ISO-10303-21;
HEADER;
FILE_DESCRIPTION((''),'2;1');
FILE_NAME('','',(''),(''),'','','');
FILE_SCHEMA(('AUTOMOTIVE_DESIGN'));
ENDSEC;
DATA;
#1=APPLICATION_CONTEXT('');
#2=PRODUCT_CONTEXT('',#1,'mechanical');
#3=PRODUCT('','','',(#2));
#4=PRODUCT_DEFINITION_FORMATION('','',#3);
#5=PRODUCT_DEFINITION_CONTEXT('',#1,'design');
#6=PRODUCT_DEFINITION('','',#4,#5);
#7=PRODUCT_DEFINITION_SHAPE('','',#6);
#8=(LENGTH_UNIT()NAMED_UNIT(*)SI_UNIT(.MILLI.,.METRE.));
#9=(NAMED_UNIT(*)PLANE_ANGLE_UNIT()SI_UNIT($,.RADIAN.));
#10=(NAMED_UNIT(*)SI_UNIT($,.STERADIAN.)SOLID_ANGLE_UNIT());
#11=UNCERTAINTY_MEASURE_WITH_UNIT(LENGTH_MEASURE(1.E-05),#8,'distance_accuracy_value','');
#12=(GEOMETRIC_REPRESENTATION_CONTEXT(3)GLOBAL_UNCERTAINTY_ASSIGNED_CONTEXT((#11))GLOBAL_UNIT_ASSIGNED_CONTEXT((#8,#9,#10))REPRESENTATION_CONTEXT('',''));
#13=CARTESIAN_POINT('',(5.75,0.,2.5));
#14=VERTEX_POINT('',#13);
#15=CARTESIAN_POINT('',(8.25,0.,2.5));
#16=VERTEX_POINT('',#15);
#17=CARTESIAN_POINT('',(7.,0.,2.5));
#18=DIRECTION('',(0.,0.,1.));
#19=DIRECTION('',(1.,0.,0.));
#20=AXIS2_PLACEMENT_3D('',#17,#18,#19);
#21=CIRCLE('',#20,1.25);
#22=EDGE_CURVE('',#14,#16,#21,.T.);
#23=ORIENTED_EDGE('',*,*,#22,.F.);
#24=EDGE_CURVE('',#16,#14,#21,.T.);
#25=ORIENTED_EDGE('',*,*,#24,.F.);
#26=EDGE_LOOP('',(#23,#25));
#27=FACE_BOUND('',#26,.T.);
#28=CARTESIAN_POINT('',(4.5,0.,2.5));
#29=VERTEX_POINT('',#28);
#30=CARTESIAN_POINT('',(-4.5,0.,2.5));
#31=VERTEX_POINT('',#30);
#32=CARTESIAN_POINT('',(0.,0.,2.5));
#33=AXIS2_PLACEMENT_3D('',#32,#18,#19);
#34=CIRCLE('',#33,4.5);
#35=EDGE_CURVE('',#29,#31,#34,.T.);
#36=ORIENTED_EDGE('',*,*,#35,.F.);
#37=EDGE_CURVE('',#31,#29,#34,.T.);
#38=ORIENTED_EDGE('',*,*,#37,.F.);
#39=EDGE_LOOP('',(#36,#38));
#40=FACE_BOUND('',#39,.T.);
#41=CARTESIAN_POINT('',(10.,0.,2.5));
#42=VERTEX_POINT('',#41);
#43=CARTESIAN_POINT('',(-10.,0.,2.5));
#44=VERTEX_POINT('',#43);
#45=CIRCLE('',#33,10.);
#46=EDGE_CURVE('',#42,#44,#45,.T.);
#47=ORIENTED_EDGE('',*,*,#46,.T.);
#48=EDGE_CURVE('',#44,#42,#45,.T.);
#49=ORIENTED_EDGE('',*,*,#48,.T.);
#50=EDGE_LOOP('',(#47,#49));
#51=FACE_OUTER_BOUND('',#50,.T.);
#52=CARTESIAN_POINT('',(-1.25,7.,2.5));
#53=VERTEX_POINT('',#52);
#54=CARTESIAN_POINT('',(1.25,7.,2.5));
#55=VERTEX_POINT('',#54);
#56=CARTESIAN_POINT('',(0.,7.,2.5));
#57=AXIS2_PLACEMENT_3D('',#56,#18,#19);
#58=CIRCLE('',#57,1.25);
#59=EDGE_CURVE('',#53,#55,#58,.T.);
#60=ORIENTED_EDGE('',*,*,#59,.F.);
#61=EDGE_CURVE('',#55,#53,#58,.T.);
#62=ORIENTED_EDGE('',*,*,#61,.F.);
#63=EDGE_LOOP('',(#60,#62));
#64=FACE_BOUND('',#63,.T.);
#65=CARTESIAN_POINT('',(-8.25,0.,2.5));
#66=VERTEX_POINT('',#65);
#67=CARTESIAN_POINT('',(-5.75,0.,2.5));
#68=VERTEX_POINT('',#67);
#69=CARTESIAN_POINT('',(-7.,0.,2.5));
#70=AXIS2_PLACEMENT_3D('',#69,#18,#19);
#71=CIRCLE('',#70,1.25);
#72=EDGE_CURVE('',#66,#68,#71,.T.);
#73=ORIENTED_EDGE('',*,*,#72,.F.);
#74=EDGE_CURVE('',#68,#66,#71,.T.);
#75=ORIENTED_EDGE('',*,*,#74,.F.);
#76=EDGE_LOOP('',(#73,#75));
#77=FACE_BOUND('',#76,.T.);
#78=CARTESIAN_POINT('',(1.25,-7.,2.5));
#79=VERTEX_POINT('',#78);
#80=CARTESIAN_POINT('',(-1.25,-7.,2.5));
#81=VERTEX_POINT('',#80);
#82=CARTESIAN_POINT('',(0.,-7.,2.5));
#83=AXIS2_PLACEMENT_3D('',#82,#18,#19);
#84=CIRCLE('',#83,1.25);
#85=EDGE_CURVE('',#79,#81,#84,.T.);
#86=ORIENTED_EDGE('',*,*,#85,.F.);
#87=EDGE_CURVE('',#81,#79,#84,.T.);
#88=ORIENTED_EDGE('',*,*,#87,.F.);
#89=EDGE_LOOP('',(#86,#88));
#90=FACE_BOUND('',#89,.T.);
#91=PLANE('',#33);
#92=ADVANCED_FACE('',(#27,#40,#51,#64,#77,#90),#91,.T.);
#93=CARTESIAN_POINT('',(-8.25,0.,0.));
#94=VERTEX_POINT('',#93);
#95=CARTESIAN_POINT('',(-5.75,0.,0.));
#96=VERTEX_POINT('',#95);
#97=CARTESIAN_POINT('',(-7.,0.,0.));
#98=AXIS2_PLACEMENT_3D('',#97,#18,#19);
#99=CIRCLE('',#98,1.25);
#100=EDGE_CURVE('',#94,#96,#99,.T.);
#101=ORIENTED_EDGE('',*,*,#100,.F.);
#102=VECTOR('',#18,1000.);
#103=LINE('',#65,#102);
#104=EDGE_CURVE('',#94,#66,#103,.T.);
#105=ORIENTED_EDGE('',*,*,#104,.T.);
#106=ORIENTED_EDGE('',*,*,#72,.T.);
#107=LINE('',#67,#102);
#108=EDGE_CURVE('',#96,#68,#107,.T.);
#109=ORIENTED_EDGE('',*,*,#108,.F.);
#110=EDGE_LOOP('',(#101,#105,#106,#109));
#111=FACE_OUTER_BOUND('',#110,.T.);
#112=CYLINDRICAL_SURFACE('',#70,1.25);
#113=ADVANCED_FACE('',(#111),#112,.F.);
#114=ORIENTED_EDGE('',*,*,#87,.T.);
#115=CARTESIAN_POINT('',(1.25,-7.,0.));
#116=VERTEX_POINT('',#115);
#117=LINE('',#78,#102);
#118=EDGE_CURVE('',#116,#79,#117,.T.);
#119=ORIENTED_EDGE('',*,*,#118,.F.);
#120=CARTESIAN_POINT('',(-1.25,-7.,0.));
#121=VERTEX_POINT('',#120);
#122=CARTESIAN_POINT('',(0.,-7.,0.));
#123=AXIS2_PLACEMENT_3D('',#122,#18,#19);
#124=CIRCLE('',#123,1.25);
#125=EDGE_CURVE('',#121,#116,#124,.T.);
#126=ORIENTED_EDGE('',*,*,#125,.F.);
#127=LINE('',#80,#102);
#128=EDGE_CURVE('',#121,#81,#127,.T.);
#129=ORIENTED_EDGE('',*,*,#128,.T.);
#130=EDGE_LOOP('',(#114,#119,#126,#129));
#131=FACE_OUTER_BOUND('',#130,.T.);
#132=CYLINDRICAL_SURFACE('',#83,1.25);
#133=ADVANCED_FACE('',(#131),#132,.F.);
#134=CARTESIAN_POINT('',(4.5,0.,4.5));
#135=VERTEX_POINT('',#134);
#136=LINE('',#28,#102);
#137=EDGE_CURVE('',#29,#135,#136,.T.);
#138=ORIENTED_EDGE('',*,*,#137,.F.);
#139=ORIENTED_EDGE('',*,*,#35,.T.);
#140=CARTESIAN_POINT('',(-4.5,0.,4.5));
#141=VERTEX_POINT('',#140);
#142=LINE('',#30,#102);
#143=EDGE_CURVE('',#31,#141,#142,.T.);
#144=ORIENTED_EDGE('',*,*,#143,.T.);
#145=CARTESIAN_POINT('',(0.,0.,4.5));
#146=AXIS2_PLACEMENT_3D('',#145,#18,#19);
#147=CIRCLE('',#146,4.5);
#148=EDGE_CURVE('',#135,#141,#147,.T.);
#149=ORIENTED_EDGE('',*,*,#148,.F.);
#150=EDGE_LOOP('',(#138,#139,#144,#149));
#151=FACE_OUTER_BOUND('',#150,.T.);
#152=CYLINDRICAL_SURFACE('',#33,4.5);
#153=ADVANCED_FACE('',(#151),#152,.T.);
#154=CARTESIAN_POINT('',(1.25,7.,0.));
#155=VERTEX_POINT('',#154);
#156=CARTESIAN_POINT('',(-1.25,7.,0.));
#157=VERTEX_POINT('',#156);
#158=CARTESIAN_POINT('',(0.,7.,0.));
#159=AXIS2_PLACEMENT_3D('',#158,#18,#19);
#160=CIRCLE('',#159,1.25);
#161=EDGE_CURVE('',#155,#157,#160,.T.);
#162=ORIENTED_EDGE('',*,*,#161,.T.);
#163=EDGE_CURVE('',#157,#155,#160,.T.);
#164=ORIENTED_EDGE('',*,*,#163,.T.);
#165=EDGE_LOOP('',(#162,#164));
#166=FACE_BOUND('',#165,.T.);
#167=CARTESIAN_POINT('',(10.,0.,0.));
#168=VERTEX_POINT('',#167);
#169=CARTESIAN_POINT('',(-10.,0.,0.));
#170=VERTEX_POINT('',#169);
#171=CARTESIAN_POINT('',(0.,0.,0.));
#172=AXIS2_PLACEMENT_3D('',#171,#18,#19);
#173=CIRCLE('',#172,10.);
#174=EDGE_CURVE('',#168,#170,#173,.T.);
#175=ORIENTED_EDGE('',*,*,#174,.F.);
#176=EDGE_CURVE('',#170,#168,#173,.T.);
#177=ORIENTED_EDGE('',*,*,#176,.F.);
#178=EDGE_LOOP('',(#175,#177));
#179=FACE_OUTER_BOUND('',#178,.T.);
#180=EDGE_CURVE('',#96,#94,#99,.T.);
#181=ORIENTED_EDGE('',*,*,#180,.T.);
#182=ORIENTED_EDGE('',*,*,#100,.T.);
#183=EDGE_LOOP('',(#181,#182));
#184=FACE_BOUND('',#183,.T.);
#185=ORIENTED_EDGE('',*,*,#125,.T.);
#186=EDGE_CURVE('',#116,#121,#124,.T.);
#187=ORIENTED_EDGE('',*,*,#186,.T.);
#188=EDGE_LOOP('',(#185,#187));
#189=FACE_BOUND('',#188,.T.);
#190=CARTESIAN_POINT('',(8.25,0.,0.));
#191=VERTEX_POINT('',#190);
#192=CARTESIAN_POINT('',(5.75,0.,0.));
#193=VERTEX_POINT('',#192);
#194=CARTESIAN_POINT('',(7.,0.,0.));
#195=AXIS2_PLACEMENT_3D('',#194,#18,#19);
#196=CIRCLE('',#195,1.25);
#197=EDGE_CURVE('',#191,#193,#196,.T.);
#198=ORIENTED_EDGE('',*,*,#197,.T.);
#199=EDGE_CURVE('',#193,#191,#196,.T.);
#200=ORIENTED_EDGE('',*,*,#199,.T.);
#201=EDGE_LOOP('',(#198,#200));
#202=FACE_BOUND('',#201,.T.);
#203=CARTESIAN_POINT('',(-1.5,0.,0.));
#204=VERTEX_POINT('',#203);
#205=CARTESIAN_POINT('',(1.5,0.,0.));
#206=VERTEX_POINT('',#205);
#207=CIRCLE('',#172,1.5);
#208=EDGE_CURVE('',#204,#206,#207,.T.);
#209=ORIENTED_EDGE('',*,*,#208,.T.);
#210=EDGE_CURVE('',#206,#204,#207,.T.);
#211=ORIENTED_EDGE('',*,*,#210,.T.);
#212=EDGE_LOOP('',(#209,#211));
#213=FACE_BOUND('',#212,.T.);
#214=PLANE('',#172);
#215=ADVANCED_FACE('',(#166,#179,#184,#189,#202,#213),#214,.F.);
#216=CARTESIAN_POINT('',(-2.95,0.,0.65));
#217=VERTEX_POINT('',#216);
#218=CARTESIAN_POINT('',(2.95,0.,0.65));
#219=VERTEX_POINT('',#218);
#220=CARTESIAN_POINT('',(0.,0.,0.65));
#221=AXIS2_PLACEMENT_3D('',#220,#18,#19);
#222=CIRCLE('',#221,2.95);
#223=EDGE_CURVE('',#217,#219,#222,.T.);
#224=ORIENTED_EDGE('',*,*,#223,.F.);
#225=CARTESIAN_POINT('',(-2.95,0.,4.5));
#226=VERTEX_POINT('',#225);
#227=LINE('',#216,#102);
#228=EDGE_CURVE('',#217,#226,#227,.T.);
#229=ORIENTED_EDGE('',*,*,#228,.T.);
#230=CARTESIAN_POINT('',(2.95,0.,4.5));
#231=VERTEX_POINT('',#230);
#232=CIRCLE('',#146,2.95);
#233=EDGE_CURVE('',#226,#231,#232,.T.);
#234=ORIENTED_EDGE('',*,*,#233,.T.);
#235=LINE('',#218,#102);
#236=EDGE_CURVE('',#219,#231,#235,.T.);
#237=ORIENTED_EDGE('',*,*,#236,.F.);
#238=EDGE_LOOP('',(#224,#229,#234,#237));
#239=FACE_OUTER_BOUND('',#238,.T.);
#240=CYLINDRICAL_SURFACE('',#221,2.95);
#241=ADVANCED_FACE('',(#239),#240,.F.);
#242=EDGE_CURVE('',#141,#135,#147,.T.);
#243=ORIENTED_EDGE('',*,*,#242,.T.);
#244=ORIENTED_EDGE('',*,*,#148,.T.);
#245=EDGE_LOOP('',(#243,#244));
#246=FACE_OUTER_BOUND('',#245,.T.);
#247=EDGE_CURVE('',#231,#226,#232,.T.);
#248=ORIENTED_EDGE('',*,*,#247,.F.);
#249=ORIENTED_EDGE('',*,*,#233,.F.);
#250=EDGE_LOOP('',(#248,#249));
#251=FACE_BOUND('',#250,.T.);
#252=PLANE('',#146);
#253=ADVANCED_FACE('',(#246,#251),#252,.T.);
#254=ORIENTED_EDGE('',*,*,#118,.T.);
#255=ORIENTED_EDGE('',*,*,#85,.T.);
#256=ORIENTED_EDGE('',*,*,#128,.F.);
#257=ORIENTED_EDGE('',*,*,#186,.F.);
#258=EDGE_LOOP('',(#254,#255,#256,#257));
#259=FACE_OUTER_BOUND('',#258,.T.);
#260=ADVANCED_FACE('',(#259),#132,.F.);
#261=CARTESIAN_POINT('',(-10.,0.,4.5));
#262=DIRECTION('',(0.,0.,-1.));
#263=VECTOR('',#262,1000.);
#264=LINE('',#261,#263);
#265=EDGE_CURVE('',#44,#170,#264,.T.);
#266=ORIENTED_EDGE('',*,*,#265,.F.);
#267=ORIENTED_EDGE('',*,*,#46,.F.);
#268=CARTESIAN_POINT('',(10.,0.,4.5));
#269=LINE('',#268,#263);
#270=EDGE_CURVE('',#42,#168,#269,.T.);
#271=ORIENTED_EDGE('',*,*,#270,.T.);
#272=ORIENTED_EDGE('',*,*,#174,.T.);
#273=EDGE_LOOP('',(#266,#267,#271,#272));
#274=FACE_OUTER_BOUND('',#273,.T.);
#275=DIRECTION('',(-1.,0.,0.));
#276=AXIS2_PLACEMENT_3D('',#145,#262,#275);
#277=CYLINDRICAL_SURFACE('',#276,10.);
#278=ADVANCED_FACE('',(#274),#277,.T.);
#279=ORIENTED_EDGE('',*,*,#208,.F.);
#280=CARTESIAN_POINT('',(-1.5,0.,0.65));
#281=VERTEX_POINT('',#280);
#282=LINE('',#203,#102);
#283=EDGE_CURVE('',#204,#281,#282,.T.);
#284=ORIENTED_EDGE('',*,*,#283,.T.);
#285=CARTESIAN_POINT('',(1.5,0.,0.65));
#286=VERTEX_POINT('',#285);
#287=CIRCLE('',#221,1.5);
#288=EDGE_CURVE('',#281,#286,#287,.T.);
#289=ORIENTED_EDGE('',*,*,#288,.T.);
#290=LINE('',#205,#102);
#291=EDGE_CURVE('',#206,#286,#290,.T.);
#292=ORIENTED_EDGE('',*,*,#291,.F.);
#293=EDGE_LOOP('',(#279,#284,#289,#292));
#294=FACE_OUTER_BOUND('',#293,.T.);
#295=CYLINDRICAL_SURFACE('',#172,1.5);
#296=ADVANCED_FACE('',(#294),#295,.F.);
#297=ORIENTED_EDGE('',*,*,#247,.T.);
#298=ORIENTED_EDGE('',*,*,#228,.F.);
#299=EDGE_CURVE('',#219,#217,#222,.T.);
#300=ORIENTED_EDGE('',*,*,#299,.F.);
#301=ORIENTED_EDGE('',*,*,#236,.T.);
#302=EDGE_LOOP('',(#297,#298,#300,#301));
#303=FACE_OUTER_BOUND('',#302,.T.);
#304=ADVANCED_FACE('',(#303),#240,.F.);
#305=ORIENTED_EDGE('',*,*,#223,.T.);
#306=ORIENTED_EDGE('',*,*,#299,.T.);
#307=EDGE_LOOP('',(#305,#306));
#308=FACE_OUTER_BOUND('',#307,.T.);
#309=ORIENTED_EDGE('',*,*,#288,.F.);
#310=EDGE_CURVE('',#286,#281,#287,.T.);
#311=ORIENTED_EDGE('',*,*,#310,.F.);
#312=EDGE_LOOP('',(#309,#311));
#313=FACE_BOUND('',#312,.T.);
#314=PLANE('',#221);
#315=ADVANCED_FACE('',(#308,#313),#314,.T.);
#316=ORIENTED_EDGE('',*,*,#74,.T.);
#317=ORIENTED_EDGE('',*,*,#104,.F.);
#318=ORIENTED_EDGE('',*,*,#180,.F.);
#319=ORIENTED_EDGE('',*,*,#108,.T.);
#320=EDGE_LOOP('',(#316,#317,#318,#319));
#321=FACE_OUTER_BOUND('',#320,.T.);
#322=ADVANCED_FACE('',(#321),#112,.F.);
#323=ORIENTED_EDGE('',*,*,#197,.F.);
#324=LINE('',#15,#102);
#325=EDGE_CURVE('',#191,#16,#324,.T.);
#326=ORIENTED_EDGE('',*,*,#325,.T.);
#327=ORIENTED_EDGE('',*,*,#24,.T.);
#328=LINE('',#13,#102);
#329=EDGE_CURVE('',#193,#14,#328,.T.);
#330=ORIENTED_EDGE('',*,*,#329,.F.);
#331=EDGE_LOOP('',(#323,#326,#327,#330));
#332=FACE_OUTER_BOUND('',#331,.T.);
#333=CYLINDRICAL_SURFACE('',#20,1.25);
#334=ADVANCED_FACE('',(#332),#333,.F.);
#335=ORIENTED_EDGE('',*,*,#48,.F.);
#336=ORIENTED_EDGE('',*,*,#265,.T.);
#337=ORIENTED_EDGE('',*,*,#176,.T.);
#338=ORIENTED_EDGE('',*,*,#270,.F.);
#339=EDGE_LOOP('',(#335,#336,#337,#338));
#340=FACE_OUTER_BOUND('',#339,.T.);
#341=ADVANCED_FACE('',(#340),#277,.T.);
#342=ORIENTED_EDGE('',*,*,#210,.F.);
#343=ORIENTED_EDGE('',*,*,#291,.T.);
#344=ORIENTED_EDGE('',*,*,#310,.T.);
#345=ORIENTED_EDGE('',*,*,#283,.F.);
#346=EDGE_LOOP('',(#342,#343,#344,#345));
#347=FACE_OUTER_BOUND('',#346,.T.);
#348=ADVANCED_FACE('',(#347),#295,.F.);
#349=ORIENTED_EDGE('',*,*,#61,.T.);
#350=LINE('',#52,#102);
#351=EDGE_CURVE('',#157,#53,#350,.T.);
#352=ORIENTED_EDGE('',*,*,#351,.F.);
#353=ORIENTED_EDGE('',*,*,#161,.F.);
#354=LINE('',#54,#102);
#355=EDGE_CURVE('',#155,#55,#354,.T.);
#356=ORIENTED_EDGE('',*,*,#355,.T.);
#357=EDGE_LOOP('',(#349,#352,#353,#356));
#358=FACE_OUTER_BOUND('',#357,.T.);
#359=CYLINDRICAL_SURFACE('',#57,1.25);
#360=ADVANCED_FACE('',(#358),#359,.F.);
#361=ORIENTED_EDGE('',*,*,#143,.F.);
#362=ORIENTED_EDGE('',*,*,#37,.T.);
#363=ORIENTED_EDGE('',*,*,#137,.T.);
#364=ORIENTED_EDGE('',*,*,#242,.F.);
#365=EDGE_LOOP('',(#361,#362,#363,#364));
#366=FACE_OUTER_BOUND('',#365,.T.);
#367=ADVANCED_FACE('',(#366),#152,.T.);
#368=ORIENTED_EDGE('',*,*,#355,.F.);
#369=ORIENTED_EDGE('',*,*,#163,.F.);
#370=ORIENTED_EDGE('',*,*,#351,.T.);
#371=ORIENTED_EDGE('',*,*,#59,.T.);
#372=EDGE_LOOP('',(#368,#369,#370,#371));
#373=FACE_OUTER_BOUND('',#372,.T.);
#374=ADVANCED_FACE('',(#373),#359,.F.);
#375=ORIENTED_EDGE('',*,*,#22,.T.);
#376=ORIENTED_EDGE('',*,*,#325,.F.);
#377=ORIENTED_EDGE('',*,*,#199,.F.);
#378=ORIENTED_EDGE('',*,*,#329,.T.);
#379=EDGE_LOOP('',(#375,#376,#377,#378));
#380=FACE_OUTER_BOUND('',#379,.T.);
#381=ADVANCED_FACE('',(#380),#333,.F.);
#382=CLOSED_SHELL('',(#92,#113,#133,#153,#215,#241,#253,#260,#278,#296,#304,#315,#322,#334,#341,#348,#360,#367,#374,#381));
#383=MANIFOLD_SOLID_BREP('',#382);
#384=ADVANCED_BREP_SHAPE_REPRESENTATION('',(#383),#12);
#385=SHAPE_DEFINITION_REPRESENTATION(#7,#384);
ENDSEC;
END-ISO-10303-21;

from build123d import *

# Parameters (mm, degrees)
SKETCH1_R           = 10
BOSS_EXTRUDE1_DEPTH = 4.5
CUT_EXTRUDE1_START  = -2
SKETCH2_R           = 10
SKETCH2_R_2         = 4.5
CUT_EXTRUDE1_DEPTH  = 2
SKETCH3_R           = 0.75
CUT_EXTRUDE2_DEPTH  = 15.361406616
SKETCH4_R           = 2.95
CUT_EXTRUDE3_DEPTH  = 3.85
SKETCH5_R           = 1.5
CUT_EXTRUDE4_DEPTH  = 15.656824349
M3_TAPPED_HOLE2_D   = 2.5


with BuildPart() as part:
    # Sketch1 → Boss-Extrude1 (new body)
    with BuildSketch(Plane.XY):
        Circle(SKETCH1_R)
    extrude(amount=BOSS_EXTRUDE1_DEPTH)

    # Sketch2 → Cut-Extrude1 (cut)
    with BuildSketch(Plane.XY.offset(4.5).offset(CUT_EXTRUDE1_START)):
        Circle(SKETCH2_R)
        Circle(SKETCH2_R_2, mode=Mode.SUBTRACT)
    extrude(amount=CUT_EXTRUDE1_DEPTH, mode=Mode.SUBTRACT)

    # Sketch3 → Cut-Extrude2 (cut, through all)
    with BuildSketch(Plane.XY.offset(2.5)):
        with Locations((0, 7)):
            Circle(SKETCH3_R)
        with Locations((7, 0)):
            Circle(SKETCH3_R)
        with Locations((0, -7)):
            Circle(SKETCH3_R)
        with Locations((-7, 0)):
            Circle(SKETCH3_R)
    extrude(amount=-CUT_EXTRUDE2_DEPTH, mode=Mode.SUBTRACT)

    # Sketch4 → Cut-Extrude3 (cut)
    with BuildSketch(Plane.XY.offset(4.5)):
        Circle(SKETCH4_R)
    extrude(amount=-CUT_EXTRUDE3_DEPTH, mode=Mode.SUBTRACT)

    # Sketch5 → Cut-Extrude4 (cut, through all)
    with BuildSketch(Plane.XY.offset(0.65)):
        Circle(SKETCH5_R)
    extrude(amount=-CUT_EXTRUDE4_DEPTH, mode=Mode.SUBTRACT)

    # M3 Tapped Hole2 (through all)
    with Locations(Plane.XY.offset(2.5)):
        with Locations((-7, 0), (0, 7), (7, 0), (0, -7)):
            Hole(M3_TAPPED_HOLE2_D / 2)


solid = part.part
